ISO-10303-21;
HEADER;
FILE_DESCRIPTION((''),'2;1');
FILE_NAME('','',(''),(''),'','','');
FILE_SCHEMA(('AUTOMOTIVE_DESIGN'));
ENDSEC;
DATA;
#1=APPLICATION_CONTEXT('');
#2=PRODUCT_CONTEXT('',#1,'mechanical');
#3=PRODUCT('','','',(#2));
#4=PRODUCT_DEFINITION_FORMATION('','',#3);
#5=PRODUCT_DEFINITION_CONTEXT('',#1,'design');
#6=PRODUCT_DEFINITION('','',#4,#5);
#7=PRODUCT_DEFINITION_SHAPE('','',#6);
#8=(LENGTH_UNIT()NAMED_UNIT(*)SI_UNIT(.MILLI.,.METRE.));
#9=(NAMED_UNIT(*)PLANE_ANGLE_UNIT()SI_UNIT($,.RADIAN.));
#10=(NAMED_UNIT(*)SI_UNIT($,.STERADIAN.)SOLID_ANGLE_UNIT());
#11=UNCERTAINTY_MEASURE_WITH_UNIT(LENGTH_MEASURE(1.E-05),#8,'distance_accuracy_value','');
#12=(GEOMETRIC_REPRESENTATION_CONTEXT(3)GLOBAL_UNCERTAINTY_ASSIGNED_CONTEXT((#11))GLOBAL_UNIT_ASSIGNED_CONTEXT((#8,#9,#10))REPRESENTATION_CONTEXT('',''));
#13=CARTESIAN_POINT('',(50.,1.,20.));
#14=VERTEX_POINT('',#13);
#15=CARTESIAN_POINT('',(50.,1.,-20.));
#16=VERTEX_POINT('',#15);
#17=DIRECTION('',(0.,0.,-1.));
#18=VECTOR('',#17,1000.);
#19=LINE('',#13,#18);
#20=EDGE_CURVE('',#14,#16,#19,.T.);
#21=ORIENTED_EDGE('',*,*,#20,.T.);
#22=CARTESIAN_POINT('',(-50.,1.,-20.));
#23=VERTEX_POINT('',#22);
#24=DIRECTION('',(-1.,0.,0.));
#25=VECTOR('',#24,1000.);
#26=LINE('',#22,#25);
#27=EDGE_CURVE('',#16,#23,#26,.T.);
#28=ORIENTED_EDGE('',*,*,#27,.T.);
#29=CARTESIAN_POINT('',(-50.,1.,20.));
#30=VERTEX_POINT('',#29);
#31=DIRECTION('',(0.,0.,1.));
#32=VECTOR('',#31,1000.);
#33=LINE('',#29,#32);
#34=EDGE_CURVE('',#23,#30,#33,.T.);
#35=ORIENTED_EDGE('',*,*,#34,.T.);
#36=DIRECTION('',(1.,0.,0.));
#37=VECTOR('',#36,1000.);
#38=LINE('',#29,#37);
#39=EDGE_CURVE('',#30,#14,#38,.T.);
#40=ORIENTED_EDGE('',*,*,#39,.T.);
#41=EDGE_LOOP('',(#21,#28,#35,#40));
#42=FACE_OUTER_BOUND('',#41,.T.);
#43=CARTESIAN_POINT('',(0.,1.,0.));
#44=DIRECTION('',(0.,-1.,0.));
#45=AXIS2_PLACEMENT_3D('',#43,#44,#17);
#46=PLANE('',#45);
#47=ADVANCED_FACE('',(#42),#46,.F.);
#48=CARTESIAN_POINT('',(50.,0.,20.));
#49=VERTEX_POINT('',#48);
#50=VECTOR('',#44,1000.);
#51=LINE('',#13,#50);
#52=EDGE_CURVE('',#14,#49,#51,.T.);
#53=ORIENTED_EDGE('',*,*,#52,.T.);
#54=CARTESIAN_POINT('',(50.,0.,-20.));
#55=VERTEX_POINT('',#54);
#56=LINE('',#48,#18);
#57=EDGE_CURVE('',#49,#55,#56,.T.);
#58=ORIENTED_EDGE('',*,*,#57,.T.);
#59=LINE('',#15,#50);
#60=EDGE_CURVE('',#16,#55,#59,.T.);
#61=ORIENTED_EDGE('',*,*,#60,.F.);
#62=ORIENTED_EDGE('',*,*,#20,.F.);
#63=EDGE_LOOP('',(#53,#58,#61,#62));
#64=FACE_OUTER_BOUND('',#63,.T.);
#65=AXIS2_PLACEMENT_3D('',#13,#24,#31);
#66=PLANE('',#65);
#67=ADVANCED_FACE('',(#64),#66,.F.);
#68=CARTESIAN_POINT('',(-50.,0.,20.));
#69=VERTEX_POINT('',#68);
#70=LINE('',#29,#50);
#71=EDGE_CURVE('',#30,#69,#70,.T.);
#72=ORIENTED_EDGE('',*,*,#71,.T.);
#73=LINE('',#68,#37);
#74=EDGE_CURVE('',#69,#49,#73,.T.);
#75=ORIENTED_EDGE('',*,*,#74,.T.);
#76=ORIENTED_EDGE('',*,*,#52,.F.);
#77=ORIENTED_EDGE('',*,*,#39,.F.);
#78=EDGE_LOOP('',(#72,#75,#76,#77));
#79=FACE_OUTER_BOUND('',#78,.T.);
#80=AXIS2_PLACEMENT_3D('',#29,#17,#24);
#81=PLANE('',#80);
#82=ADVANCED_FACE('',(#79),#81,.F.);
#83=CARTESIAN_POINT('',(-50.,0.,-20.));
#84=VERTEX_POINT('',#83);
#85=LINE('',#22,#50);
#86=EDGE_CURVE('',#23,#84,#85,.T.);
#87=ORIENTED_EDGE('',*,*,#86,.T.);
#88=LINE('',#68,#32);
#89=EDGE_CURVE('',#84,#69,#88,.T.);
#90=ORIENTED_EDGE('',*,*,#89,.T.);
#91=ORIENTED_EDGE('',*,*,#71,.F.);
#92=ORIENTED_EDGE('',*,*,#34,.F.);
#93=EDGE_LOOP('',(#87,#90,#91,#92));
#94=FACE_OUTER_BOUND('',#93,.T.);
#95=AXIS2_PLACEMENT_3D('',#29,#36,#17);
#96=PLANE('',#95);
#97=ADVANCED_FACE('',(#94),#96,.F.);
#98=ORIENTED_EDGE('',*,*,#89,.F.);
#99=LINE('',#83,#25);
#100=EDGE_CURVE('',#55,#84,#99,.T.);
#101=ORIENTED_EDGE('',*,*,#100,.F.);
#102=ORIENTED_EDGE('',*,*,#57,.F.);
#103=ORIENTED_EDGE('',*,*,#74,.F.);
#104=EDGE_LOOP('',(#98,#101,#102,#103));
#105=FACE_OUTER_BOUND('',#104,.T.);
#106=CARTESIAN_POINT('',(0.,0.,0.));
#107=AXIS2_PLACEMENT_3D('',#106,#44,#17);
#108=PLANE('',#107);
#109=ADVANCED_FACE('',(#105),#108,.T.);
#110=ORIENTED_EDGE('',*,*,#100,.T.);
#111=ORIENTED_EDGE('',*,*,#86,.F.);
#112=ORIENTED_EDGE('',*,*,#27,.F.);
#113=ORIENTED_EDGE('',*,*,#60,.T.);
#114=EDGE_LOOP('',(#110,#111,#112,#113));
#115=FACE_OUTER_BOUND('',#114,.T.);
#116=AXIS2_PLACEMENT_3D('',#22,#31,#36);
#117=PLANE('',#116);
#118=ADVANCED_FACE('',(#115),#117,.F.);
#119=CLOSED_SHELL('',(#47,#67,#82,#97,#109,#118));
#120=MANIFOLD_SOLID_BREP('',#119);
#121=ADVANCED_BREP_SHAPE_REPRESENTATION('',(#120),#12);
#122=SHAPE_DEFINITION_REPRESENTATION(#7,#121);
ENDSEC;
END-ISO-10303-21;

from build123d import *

# Parameters (mm, degrees)
SKETCH_1_W      = 100
SKETCH_1_H      = 40
EXTRUDE_1_DEPTH = 1


with BuildPart() as part:
    # 草图1 → 凸台-拉伸1 (new body)
    with BuildSketch(Plane(origin=(0, 0, 0), x_dir=(1, 0, 0), z_dir=(0, 1, 0))):
        Rectangle(SKETCH_1_W, SKETCH_1_H)
    extrude(amount=EXTRUDE_1_DEPTH)


solid = part.part
